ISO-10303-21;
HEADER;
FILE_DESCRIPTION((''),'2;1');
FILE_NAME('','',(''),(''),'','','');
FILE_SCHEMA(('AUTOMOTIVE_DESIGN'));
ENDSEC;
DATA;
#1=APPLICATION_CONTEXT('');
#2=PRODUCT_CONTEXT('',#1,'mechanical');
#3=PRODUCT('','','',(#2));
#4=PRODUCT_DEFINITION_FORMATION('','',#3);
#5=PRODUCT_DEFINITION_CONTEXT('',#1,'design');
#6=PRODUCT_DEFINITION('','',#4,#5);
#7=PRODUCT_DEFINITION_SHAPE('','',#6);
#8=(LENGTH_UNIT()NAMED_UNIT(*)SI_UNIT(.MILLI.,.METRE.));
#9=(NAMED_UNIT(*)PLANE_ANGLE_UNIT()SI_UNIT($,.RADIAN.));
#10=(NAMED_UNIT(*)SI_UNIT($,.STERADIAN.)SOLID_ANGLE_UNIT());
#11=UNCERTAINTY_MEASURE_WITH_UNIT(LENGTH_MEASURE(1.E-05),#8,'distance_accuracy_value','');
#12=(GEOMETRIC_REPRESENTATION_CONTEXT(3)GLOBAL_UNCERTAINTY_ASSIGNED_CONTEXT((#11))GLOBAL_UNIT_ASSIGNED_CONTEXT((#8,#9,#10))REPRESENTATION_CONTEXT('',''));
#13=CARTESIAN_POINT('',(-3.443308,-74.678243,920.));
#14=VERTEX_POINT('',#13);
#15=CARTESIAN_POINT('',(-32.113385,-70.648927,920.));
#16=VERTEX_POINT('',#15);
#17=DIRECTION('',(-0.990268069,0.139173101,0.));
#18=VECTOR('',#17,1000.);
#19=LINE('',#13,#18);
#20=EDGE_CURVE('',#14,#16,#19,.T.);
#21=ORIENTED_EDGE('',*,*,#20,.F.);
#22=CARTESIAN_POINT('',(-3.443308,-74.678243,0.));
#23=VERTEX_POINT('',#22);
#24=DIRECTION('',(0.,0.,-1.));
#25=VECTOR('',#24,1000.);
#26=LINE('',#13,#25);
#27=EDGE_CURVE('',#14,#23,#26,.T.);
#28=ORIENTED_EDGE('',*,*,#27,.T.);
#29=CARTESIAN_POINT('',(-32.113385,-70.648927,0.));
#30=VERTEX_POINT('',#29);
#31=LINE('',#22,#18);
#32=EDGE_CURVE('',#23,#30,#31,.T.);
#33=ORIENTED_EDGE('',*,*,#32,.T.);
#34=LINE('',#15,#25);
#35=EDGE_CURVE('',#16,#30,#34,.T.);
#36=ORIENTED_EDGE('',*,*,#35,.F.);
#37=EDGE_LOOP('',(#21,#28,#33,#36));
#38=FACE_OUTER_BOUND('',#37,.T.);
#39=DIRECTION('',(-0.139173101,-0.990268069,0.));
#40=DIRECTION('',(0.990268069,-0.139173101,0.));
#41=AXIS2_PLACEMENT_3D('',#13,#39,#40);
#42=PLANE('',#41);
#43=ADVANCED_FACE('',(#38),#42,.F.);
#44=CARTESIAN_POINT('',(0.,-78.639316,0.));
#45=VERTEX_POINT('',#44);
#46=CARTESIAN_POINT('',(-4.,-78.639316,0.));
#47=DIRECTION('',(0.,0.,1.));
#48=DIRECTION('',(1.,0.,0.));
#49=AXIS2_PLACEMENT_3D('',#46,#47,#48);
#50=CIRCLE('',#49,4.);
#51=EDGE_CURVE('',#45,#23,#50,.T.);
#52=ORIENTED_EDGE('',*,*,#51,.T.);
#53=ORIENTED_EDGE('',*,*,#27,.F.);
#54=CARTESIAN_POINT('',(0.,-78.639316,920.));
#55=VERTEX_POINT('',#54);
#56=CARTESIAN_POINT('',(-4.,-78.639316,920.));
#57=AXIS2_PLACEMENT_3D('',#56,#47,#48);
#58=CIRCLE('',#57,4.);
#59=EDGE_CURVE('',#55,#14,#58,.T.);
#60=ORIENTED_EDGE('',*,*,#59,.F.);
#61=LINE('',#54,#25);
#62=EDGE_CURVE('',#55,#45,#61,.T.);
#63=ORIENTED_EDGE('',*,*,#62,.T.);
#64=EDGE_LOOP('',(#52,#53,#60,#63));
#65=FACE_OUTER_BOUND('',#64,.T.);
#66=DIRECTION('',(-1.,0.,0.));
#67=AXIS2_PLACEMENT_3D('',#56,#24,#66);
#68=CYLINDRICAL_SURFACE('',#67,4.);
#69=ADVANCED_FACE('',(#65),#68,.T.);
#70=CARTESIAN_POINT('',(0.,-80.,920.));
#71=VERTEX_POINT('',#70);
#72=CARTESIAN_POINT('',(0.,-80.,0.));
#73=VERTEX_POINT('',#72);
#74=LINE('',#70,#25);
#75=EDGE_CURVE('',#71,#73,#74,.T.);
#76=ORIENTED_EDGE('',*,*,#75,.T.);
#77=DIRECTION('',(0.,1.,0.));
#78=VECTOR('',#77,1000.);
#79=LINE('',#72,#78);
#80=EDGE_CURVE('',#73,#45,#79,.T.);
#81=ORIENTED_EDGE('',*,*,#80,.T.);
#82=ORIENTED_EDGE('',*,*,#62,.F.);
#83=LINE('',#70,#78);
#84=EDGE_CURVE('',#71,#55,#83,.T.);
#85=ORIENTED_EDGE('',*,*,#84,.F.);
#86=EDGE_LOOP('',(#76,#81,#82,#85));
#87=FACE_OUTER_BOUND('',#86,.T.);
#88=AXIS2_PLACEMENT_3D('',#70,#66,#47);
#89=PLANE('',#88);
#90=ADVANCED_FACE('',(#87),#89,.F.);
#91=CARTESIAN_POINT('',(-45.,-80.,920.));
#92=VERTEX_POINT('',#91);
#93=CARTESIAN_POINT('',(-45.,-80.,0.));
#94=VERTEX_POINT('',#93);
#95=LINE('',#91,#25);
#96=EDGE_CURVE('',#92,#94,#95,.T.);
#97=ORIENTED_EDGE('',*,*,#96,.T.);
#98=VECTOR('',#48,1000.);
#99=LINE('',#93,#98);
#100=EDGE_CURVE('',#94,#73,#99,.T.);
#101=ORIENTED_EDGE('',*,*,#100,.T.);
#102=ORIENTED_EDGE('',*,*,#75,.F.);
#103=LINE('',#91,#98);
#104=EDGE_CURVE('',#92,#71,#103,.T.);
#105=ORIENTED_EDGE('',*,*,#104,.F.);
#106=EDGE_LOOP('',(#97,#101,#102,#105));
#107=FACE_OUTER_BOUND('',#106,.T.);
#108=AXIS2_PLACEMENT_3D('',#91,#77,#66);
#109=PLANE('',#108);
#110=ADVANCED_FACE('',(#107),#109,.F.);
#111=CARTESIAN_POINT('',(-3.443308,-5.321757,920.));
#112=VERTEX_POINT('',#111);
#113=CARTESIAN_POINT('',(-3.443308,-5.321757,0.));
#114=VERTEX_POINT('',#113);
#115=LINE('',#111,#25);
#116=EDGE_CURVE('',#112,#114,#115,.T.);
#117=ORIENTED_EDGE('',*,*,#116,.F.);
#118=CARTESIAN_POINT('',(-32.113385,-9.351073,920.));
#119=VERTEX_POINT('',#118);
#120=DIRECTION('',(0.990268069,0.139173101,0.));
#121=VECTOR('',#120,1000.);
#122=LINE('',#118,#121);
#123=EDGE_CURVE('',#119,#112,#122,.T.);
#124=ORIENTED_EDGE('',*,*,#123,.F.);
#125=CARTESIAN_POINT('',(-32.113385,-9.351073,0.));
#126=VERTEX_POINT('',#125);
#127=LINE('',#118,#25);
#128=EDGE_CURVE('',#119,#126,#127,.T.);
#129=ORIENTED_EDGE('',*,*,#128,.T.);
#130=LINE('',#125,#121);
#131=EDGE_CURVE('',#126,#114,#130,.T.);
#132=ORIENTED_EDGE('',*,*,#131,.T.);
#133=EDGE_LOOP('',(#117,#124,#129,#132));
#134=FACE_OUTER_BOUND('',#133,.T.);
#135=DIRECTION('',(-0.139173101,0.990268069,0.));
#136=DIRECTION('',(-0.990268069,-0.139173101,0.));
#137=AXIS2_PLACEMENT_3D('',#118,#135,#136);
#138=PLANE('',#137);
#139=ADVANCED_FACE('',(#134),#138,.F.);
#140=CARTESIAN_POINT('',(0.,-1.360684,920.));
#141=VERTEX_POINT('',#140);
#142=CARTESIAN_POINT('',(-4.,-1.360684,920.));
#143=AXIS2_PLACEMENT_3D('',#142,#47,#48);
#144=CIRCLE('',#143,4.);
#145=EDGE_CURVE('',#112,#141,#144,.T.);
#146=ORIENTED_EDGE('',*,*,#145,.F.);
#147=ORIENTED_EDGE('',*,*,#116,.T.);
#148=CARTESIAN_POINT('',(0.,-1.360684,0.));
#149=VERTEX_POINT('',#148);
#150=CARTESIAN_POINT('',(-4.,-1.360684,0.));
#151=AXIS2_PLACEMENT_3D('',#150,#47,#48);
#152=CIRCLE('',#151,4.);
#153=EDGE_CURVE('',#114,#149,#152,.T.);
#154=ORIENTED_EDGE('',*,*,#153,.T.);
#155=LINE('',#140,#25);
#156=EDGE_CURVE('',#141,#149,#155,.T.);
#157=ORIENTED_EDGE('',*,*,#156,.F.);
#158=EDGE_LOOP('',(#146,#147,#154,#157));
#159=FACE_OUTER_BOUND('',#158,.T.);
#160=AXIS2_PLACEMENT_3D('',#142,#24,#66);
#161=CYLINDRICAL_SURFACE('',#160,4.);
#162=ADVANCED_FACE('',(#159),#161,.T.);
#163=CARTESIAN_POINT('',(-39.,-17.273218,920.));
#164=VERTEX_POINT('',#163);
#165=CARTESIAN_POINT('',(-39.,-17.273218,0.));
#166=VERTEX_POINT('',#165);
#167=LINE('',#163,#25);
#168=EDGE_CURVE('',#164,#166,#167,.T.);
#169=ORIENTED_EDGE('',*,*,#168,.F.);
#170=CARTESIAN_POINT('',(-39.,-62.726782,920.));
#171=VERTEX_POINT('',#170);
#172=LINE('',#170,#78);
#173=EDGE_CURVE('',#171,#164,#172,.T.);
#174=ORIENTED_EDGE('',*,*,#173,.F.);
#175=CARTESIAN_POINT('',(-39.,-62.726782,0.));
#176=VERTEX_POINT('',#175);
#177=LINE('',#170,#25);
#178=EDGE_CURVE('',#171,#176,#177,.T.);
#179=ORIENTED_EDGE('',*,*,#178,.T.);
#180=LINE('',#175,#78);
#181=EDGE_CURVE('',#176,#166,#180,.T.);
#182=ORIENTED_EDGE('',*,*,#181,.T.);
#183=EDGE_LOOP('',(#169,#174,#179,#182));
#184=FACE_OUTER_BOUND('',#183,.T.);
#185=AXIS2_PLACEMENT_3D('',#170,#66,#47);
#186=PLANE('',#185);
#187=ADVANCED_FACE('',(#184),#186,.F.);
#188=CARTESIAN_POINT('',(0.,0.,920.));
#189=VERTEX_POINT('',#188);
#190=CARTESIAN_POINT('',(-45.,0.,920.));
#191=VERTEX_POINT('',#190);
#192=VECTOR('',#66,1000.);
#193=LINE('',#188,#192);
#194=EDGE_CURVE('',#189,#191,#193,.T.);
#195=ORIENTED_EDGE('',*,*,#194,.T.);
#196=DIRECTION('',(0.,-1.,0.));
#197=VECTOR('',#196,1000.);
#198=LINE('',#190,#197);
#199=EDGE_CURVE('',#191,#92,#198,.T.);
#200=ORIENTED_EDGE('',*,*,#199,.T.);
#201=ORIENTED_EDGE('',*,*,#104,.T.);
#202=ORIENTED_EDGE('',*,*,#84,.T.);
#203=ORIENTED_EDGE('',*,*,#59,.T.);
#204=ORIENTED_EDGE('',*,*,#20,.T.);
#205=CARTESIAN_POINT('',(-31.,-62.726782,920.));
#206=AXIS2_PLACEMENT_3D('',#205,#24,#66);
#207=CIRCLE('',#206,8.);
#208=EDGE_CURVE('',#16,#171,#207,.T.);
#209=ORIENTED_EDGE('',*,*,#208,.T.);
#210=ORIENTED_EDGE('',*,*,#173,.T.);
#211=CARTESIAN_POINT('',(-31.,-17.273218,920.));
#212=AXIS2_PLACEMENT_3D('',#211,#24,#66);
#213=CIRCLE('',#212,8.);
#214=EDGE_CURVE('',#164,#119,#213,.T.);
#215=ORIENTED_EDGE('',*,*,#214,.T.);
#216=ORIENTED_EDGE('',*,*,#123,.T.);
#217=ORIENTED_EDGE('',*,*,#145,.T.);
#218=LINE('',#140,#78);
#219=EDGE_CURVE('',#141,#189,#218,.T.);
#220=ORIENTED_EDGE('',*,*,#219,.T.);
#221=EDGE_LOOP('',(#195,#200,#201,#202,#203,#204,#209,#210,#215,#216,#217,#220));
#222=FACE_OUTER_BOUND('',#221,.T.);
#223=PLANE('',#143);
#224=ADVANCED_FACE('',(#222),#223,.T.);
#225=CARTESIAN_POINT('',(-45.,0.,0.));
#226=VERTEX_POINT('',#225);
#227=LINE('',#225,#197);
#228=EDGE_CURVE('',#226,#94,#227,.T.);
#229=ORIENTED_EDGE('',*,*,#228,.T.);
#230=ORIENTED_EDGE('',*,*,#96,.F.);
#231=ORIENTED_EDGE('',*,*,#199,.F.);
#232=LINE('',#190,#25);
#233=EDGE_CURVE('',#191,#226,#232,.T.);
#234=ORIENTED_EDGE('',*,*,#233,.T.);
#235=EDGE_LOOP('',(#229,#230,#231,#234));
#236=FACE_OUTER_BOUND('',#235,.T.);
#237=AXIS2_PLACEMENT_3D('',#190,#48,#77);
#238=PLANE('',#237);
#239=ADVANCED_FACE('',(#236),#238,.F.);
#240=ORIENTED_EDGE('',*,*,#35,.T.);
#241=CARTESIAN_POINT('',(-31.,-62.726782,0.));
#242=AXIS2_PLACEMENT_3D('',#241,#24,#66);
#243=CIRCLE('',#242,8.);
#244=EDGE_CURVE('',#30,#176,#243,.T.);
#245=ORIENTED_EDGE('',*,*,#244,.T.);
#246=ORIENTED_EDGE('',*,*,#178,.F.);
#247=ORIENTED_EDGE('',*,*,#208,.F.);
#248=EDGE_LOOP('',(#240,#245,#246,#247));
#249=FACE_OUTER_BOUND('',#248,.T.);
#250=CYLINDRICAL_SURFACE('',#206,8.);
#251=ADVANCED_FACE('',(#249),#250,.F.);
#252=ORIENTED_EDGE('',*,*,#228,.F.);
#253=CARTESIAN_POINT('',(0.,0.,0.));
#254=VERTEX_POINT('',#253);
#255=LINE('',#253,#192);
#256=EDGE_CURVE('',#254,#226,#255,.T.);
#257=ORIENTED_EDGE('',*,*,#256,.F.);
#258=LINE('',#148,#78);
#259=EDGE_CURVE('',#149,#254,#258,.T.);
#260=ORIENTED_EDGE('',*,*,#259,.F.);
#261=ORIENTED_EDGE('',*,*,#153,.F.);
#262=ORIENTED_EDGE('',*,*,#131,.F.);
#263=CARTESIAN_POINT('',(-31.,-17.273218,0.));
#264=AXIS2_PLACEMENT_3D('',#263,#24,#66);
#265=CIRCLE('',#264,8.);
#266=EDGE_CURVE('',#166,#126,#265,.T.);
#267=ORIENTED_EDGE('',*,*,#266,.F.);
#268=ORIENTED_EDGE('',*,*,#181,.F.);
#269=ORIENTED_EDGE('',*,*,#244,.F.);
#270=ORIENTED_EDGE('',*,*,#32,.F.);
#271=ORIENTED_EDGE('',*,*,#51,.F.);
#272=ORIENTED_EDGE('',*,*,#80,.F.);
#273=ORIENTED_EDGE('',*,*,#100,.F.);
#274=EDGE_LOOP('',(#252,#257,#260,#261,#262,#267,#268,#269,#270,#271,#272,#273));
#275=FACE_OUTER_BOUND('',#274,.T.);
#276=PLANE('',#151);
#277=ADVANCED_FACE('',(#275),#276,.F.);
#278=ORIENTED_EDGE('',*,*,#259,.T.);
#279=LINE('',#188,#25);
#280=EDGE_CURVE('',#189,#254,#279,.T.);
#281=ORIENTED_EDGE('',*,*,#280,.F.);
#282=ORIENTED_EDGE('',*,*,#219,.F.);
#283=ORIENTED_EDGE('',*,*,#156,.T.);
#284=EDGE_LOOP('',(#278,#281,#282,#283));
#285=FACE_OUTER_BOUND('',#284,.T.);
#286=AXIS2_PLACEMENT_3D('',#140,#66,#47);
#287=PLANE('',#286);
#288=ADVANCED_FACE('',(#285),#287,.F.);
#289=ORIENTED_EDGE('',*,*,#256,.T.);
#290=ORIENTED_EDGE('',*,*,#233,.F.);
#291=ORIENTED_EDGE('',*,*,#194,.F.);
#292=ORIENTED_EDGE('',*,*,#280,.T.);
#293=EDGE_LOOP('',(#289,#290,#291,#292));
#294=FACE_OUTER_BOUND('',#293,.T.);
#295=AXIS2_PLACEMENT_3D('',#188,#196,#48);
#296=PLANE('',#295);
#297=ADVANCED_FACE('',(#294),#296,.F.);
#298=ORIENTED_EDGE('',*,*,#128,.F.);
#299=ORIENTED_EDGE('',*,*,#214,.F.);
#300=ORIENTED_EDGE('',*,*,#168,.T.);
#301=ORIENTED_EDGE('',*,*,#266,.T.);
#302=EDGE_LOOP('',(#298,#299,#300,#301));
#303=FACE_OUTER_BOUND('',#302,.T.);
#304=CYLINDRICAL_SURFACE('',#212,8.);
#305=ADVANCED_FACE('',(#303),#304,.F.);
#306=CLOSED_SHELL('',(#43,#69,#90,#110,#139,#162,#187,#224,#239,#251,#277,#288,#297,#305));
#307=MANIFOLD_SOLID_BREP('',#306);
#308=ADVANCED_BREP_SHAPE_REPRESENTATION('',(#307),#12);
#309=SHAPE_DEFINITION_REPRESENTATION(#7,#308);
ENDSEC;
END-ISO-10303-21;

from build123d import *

# Parameters (mm, degrees)
BOSS_EXTRUDE1_DEPTH = 920


with BuildPart() as part:
    # Sketch1 → Boss-Extrude1 (new body)
    with BuildSketch(Plane.XY):
        with BuildLine():
            Line((0, 0), (-45, 0))
            Line((-45, 0), (-45, -80))
            Line((-45, -80), (0, -80))
            Line((0, -80), (0, -78.639315732))
            ThreePointArc((0, -78.639315732), (-0.981161679, -76.015079616), (-3.443307596, -74.678243457))
            Line((-3.443307596, -74.678243457), (-32.113384808, -70.648926875))
            ThreePointArc((-32.113384808, -70.648926875), (-37.037676642, -67.975254557), (-39, -62.726782325))
            Line((-39, -62.726782325), (-39, -17.273217675))
            ThreePointArc((-39, -17.273217675), (-37.037676642, -12.024745443), (-32.113384808, -9.351073125))
            Line((-32.113384808, -9.351073125), (-3.443307596, -5.321756543))
            ThreePointArc((-3.443307596, -5.321756543), (-0.981161679, -3.984920384), (0, -1.360684268))
            Line((0, -1.360684268), (0, 0))
        make_face()
    extrude(amount=BOSS_EXTRUDE1_DEPTH)


solid = part.part
